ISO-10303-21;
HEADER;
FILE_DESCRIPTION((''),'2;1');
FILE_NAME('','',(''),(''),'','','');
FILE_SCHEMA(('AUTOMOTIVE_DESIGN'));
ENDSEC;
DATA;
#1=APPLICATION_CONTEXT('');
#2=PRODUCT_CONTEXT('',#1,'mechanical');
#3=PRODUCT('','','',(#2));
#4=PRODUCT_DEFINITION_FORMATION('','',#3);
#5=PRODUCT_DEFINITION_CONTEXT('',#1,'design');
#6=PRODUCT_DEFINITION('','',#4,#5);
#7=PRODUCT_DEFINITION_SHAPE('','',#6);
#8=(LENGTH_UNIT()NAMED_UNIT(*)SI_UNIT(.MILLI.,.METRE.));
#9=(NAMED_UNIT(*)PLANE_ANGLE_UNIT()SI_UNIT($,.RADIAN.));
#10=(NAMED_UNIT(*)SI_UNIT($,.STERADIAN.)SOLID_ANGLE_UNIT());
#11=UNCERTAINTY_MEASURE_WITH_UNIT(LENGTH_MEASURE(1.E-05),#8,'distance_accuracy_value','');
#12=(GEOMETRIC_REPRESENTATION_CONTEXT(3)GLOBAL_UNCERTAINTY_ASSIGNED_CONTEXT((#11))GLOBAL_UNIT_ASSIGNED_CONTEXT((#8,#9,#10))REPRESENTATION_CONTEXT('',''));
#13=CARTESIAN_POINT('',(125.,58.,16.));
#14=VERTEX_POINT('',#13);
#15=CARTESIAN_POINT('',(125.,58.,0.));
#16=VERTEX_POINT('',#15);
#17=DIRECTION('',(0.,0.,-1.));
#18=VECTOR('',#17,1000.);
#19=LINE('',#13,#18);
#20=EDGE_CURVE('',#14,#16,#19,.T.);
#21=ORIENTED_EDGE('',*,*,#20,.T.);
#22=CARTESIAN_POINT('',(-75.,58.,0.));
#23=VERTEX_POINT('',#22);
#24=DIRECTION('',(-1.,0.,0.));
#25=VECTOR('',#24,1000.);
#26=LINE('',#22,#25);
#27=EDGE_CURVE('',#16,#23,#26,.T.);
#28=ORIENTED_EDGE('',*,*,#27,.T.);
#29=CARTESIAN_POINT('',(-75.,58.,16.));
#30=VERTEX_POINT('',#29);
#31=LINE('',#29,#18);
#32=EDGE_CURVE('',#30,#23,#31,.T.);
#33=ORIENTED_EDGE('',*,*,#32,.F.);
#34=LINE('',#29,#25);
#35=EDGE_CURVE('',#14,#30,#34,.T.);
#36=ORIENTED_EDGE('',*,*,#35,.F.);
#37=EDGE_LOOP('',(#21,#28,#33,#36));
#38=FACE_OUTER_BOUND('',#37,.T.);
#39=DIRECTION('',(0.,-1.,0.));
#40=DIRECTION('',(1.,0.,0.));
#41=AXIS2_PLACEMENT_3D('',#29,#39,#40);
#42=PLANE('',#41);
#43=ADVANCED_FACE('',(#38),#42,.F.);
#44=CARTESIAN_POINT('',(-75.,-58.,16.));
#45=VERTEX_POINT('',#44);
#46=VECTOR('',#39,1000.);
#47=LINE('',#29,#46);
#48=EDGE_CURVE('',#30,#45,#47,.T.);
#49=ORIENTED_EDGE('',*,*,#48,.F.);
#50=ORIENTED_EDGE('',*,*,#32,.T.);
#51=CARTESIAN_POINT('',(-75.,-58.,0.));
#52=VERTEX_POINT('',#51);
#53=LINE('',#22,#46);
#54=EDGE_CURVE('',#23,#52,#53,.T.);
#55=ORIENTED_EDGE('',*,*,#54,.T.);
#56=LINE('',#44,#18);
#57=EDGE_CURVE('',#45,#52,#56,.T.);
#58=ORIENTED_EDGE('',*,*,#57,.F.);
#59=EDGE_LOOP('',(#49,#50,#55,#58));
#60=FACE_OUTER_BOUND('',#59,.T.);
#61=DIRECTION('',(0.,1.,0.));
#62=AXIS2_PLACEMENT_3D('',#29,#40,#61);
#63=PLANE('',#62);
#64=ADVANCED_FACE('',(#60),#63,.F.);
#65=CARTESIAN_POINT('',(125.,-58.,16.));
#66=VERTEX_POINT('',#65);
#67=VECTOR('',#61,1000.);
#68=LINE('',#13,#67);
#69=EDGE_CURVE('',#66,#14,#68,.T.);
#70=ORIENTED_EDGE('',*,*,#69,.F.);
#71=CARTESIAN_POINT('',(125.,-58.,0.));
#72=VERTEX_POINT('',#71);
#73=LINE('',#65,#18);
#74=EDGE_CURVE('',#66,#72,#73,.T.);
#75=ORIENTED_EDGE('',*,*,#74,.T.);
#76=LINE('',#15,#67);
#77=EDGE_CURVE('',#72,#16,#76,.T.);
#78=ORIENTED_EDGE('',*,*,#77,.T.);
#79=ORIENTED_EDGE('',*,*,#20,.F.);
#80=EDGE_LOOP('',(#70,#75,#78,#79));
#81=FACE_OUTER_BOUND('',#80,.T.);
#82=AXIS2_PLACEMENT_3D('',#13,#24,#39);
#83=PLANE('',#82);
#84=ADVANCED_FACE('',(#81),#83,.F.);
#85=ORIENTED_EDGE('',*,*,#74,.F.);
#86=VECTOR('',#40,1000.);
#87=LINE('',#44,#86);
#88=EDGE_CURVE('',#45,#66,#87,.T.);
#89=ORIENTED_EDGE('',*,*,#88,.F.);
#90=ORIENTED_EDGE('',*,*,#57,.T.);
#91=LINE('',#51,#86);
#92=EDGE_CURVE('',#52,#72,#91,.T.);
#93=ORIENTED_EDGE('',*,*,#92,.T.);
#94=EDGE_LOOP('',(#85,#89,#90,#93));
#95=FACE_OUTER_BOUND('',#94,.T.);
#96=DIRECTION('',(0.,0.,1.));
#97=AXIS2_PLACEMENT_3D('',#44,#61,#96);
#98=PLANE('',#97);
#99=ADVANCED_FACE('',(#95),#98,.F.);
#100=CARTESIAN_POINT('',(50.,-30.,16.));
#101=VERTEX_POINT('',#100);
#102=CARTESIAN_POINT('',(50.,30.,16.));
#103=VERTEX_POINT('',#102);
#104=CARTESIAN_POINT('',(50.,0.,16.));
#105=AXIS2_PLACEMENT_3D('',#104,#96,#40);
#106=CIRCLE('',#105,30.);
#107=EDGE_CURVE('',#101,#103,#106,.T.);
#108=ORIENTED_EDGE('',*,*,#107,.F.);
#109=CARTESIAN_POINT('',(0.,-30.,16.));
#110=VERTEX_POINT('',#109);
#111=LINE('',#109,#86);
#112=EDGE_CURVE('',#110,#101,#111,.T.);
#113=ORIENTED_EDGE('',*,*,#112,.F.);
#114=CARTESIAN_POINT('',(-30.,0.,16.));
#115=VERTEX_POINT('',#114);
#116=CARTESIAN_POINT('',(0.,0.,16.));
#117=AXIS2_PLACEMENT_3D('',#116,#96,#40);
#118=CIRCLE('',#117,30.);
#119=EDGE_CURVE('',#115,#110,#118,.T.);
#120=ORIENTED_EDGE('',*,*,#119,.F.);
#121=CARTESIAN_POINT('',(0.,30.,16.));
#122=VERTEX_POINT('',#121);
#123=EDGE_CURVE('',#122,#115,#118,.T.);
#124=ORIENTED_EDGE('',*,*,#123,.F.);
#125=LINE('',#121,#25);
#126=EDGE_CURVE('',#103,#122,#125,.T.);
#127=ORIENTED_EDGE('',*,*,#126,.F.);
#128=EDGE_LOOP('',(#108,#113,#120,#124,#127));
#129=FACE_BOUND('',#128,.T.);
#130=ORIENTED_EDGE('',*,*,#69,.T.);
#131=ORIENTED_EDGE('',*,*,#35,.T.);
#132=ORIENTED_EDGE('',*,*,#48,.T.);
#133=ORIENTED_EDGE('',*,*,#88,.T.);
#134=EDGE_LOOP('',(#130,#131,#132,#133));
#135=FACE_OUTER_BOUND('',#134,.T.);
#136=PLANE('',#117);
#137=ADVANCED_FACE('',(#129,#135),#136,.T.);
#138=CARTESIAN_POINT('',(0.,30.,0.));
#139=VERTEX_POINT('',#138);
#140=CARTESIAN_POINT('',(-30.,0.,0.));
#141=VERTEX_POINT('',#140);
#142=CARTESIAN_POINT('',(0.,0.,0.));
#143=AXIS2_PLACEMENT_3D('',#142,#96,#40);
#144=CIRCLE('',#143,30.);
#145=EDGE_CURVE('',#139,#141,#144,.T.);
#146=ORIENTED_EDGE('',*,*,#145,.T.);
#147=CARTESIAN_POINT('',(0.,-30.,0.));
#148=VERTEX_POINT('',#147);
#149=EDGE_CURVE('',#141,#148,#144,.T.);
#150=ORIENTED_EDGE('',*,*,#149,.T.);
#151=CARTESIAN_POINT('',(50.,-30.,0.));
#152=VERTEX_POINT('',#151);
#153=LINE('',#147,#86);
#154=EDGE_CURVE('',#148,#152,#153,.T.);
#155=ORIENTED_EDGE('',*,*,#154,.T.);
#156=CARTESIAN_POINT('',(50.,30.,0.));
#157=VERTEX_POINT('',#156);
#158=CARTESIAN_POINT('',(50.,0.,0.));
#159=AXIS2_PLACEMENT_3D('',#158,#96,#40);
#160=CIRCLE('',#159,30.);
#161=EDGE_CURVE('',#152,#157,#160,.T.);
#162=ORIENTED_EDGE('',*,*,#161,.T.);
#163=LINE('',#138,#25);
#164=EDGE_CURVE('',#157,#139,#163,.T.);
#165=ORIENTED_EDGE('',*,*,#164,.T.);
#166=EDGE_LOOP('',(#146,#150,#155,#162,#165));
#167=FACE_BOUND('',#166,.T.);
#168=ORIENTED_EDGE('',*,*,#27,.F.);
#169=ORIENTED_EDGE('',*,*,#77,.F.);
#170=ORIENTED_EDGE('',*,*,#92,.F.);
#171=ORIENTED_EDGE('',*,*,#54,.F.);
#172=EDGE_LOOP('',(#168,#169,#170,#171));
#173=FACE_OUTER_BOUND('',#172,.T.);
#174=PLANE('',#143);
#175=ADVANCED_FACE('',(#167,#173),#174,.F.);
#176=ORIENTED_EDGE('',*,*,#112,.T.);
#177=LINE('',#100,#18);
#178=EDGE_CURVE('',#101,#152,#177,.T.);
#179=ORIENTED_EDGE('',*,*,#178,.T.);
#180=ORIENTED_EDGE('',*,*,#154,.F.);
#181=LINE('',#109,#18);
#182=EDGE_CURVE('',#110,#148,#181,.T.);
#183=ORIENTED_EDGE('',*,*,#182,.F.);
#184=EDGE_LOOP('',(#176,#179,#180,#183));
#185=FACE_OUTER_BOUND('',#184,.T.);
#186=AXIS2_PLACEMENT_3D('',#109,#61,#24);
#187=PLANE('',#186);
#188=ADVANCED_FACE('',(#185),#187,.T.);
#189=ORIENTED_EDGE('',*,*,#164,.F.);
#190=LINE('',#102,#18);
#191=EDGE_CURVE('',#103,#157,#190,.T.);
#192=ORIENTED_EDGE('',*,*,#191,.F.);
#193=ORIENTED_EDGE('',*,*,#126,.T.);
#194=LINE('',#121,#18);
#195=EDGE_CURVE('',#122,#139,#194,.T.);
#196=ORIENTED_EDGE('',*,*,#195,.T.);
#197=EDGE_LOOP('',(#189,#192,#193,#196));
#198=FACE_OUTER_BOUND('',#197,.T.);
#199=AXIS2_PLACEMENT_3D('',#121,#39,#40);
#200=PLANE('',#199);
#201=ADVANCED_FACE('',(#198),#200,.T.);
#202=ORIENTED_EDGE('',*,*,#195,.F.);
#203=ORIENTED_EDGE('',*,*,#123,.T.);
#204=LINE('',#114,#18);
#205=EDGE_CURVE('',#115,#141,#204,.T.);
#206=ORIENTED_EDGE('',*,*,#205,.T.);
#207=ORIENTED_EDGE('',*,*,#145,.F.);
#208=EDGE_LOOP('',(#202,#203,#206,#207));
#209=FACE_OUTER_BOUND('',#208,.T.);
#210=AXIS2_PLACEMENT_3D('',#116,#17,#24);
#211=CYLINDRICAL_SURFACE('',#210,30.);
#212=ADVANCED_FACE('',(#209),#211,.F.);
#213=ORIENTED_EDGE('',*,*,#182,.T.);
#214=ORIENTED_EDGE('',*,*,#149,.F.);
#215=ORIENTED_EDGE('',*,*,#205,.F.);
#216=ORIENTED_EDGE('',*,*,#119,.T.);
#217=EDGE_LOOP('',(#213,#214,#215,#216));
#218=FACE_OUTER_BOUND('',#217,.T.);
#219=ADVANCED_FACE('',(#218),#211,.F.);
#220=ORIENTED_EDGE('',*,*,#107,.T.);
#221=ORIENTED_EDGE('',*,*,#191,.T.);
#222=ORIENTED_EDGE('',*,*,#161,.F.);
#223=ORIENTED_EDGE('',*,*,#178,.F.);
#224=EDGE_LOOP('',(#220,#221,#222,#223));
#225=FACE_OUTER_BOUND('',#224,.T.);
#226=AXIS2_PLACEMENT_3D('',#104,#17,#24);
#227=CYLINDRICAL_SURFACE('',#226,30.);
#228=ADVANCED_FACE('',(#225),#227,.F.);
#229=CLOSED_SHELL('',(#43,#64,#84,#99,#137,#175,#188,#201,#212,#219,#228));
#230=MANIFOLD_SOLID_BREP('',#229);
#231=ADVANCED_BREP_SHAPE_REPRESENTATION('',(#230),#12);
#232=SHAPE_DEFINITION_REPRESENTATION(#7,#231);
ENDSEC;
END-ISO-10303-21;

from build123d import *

# Parameters (mm, degrees)
SKETCH1_W           = 200
SKETCH1_H           = 116
BOSS_EXTRUDE1_DEPTH = 16


with BuildPart() as part:
    # Sketch1 → Boss-Extrude1 (new body)
    with BuildSketch(Plane.XY):
        with Locations((25, 0)):
            Rectangle(SKETCH1_W, SKETCH1_H)
        with BuildLine():
            Line((0, 30), (50, 30))
            ThreePointArc((50, 30), (80, 0), (50, -30))
            Line((50, -30), (0, -30))
            ThreePointArc((0, -30), (-30, 0), (0, 30))
        make_face(mode=Mode.SUBTRACT)
    extrude(amount=BOSS_EXTRUDE1_DEPTH)


solid = part.part
